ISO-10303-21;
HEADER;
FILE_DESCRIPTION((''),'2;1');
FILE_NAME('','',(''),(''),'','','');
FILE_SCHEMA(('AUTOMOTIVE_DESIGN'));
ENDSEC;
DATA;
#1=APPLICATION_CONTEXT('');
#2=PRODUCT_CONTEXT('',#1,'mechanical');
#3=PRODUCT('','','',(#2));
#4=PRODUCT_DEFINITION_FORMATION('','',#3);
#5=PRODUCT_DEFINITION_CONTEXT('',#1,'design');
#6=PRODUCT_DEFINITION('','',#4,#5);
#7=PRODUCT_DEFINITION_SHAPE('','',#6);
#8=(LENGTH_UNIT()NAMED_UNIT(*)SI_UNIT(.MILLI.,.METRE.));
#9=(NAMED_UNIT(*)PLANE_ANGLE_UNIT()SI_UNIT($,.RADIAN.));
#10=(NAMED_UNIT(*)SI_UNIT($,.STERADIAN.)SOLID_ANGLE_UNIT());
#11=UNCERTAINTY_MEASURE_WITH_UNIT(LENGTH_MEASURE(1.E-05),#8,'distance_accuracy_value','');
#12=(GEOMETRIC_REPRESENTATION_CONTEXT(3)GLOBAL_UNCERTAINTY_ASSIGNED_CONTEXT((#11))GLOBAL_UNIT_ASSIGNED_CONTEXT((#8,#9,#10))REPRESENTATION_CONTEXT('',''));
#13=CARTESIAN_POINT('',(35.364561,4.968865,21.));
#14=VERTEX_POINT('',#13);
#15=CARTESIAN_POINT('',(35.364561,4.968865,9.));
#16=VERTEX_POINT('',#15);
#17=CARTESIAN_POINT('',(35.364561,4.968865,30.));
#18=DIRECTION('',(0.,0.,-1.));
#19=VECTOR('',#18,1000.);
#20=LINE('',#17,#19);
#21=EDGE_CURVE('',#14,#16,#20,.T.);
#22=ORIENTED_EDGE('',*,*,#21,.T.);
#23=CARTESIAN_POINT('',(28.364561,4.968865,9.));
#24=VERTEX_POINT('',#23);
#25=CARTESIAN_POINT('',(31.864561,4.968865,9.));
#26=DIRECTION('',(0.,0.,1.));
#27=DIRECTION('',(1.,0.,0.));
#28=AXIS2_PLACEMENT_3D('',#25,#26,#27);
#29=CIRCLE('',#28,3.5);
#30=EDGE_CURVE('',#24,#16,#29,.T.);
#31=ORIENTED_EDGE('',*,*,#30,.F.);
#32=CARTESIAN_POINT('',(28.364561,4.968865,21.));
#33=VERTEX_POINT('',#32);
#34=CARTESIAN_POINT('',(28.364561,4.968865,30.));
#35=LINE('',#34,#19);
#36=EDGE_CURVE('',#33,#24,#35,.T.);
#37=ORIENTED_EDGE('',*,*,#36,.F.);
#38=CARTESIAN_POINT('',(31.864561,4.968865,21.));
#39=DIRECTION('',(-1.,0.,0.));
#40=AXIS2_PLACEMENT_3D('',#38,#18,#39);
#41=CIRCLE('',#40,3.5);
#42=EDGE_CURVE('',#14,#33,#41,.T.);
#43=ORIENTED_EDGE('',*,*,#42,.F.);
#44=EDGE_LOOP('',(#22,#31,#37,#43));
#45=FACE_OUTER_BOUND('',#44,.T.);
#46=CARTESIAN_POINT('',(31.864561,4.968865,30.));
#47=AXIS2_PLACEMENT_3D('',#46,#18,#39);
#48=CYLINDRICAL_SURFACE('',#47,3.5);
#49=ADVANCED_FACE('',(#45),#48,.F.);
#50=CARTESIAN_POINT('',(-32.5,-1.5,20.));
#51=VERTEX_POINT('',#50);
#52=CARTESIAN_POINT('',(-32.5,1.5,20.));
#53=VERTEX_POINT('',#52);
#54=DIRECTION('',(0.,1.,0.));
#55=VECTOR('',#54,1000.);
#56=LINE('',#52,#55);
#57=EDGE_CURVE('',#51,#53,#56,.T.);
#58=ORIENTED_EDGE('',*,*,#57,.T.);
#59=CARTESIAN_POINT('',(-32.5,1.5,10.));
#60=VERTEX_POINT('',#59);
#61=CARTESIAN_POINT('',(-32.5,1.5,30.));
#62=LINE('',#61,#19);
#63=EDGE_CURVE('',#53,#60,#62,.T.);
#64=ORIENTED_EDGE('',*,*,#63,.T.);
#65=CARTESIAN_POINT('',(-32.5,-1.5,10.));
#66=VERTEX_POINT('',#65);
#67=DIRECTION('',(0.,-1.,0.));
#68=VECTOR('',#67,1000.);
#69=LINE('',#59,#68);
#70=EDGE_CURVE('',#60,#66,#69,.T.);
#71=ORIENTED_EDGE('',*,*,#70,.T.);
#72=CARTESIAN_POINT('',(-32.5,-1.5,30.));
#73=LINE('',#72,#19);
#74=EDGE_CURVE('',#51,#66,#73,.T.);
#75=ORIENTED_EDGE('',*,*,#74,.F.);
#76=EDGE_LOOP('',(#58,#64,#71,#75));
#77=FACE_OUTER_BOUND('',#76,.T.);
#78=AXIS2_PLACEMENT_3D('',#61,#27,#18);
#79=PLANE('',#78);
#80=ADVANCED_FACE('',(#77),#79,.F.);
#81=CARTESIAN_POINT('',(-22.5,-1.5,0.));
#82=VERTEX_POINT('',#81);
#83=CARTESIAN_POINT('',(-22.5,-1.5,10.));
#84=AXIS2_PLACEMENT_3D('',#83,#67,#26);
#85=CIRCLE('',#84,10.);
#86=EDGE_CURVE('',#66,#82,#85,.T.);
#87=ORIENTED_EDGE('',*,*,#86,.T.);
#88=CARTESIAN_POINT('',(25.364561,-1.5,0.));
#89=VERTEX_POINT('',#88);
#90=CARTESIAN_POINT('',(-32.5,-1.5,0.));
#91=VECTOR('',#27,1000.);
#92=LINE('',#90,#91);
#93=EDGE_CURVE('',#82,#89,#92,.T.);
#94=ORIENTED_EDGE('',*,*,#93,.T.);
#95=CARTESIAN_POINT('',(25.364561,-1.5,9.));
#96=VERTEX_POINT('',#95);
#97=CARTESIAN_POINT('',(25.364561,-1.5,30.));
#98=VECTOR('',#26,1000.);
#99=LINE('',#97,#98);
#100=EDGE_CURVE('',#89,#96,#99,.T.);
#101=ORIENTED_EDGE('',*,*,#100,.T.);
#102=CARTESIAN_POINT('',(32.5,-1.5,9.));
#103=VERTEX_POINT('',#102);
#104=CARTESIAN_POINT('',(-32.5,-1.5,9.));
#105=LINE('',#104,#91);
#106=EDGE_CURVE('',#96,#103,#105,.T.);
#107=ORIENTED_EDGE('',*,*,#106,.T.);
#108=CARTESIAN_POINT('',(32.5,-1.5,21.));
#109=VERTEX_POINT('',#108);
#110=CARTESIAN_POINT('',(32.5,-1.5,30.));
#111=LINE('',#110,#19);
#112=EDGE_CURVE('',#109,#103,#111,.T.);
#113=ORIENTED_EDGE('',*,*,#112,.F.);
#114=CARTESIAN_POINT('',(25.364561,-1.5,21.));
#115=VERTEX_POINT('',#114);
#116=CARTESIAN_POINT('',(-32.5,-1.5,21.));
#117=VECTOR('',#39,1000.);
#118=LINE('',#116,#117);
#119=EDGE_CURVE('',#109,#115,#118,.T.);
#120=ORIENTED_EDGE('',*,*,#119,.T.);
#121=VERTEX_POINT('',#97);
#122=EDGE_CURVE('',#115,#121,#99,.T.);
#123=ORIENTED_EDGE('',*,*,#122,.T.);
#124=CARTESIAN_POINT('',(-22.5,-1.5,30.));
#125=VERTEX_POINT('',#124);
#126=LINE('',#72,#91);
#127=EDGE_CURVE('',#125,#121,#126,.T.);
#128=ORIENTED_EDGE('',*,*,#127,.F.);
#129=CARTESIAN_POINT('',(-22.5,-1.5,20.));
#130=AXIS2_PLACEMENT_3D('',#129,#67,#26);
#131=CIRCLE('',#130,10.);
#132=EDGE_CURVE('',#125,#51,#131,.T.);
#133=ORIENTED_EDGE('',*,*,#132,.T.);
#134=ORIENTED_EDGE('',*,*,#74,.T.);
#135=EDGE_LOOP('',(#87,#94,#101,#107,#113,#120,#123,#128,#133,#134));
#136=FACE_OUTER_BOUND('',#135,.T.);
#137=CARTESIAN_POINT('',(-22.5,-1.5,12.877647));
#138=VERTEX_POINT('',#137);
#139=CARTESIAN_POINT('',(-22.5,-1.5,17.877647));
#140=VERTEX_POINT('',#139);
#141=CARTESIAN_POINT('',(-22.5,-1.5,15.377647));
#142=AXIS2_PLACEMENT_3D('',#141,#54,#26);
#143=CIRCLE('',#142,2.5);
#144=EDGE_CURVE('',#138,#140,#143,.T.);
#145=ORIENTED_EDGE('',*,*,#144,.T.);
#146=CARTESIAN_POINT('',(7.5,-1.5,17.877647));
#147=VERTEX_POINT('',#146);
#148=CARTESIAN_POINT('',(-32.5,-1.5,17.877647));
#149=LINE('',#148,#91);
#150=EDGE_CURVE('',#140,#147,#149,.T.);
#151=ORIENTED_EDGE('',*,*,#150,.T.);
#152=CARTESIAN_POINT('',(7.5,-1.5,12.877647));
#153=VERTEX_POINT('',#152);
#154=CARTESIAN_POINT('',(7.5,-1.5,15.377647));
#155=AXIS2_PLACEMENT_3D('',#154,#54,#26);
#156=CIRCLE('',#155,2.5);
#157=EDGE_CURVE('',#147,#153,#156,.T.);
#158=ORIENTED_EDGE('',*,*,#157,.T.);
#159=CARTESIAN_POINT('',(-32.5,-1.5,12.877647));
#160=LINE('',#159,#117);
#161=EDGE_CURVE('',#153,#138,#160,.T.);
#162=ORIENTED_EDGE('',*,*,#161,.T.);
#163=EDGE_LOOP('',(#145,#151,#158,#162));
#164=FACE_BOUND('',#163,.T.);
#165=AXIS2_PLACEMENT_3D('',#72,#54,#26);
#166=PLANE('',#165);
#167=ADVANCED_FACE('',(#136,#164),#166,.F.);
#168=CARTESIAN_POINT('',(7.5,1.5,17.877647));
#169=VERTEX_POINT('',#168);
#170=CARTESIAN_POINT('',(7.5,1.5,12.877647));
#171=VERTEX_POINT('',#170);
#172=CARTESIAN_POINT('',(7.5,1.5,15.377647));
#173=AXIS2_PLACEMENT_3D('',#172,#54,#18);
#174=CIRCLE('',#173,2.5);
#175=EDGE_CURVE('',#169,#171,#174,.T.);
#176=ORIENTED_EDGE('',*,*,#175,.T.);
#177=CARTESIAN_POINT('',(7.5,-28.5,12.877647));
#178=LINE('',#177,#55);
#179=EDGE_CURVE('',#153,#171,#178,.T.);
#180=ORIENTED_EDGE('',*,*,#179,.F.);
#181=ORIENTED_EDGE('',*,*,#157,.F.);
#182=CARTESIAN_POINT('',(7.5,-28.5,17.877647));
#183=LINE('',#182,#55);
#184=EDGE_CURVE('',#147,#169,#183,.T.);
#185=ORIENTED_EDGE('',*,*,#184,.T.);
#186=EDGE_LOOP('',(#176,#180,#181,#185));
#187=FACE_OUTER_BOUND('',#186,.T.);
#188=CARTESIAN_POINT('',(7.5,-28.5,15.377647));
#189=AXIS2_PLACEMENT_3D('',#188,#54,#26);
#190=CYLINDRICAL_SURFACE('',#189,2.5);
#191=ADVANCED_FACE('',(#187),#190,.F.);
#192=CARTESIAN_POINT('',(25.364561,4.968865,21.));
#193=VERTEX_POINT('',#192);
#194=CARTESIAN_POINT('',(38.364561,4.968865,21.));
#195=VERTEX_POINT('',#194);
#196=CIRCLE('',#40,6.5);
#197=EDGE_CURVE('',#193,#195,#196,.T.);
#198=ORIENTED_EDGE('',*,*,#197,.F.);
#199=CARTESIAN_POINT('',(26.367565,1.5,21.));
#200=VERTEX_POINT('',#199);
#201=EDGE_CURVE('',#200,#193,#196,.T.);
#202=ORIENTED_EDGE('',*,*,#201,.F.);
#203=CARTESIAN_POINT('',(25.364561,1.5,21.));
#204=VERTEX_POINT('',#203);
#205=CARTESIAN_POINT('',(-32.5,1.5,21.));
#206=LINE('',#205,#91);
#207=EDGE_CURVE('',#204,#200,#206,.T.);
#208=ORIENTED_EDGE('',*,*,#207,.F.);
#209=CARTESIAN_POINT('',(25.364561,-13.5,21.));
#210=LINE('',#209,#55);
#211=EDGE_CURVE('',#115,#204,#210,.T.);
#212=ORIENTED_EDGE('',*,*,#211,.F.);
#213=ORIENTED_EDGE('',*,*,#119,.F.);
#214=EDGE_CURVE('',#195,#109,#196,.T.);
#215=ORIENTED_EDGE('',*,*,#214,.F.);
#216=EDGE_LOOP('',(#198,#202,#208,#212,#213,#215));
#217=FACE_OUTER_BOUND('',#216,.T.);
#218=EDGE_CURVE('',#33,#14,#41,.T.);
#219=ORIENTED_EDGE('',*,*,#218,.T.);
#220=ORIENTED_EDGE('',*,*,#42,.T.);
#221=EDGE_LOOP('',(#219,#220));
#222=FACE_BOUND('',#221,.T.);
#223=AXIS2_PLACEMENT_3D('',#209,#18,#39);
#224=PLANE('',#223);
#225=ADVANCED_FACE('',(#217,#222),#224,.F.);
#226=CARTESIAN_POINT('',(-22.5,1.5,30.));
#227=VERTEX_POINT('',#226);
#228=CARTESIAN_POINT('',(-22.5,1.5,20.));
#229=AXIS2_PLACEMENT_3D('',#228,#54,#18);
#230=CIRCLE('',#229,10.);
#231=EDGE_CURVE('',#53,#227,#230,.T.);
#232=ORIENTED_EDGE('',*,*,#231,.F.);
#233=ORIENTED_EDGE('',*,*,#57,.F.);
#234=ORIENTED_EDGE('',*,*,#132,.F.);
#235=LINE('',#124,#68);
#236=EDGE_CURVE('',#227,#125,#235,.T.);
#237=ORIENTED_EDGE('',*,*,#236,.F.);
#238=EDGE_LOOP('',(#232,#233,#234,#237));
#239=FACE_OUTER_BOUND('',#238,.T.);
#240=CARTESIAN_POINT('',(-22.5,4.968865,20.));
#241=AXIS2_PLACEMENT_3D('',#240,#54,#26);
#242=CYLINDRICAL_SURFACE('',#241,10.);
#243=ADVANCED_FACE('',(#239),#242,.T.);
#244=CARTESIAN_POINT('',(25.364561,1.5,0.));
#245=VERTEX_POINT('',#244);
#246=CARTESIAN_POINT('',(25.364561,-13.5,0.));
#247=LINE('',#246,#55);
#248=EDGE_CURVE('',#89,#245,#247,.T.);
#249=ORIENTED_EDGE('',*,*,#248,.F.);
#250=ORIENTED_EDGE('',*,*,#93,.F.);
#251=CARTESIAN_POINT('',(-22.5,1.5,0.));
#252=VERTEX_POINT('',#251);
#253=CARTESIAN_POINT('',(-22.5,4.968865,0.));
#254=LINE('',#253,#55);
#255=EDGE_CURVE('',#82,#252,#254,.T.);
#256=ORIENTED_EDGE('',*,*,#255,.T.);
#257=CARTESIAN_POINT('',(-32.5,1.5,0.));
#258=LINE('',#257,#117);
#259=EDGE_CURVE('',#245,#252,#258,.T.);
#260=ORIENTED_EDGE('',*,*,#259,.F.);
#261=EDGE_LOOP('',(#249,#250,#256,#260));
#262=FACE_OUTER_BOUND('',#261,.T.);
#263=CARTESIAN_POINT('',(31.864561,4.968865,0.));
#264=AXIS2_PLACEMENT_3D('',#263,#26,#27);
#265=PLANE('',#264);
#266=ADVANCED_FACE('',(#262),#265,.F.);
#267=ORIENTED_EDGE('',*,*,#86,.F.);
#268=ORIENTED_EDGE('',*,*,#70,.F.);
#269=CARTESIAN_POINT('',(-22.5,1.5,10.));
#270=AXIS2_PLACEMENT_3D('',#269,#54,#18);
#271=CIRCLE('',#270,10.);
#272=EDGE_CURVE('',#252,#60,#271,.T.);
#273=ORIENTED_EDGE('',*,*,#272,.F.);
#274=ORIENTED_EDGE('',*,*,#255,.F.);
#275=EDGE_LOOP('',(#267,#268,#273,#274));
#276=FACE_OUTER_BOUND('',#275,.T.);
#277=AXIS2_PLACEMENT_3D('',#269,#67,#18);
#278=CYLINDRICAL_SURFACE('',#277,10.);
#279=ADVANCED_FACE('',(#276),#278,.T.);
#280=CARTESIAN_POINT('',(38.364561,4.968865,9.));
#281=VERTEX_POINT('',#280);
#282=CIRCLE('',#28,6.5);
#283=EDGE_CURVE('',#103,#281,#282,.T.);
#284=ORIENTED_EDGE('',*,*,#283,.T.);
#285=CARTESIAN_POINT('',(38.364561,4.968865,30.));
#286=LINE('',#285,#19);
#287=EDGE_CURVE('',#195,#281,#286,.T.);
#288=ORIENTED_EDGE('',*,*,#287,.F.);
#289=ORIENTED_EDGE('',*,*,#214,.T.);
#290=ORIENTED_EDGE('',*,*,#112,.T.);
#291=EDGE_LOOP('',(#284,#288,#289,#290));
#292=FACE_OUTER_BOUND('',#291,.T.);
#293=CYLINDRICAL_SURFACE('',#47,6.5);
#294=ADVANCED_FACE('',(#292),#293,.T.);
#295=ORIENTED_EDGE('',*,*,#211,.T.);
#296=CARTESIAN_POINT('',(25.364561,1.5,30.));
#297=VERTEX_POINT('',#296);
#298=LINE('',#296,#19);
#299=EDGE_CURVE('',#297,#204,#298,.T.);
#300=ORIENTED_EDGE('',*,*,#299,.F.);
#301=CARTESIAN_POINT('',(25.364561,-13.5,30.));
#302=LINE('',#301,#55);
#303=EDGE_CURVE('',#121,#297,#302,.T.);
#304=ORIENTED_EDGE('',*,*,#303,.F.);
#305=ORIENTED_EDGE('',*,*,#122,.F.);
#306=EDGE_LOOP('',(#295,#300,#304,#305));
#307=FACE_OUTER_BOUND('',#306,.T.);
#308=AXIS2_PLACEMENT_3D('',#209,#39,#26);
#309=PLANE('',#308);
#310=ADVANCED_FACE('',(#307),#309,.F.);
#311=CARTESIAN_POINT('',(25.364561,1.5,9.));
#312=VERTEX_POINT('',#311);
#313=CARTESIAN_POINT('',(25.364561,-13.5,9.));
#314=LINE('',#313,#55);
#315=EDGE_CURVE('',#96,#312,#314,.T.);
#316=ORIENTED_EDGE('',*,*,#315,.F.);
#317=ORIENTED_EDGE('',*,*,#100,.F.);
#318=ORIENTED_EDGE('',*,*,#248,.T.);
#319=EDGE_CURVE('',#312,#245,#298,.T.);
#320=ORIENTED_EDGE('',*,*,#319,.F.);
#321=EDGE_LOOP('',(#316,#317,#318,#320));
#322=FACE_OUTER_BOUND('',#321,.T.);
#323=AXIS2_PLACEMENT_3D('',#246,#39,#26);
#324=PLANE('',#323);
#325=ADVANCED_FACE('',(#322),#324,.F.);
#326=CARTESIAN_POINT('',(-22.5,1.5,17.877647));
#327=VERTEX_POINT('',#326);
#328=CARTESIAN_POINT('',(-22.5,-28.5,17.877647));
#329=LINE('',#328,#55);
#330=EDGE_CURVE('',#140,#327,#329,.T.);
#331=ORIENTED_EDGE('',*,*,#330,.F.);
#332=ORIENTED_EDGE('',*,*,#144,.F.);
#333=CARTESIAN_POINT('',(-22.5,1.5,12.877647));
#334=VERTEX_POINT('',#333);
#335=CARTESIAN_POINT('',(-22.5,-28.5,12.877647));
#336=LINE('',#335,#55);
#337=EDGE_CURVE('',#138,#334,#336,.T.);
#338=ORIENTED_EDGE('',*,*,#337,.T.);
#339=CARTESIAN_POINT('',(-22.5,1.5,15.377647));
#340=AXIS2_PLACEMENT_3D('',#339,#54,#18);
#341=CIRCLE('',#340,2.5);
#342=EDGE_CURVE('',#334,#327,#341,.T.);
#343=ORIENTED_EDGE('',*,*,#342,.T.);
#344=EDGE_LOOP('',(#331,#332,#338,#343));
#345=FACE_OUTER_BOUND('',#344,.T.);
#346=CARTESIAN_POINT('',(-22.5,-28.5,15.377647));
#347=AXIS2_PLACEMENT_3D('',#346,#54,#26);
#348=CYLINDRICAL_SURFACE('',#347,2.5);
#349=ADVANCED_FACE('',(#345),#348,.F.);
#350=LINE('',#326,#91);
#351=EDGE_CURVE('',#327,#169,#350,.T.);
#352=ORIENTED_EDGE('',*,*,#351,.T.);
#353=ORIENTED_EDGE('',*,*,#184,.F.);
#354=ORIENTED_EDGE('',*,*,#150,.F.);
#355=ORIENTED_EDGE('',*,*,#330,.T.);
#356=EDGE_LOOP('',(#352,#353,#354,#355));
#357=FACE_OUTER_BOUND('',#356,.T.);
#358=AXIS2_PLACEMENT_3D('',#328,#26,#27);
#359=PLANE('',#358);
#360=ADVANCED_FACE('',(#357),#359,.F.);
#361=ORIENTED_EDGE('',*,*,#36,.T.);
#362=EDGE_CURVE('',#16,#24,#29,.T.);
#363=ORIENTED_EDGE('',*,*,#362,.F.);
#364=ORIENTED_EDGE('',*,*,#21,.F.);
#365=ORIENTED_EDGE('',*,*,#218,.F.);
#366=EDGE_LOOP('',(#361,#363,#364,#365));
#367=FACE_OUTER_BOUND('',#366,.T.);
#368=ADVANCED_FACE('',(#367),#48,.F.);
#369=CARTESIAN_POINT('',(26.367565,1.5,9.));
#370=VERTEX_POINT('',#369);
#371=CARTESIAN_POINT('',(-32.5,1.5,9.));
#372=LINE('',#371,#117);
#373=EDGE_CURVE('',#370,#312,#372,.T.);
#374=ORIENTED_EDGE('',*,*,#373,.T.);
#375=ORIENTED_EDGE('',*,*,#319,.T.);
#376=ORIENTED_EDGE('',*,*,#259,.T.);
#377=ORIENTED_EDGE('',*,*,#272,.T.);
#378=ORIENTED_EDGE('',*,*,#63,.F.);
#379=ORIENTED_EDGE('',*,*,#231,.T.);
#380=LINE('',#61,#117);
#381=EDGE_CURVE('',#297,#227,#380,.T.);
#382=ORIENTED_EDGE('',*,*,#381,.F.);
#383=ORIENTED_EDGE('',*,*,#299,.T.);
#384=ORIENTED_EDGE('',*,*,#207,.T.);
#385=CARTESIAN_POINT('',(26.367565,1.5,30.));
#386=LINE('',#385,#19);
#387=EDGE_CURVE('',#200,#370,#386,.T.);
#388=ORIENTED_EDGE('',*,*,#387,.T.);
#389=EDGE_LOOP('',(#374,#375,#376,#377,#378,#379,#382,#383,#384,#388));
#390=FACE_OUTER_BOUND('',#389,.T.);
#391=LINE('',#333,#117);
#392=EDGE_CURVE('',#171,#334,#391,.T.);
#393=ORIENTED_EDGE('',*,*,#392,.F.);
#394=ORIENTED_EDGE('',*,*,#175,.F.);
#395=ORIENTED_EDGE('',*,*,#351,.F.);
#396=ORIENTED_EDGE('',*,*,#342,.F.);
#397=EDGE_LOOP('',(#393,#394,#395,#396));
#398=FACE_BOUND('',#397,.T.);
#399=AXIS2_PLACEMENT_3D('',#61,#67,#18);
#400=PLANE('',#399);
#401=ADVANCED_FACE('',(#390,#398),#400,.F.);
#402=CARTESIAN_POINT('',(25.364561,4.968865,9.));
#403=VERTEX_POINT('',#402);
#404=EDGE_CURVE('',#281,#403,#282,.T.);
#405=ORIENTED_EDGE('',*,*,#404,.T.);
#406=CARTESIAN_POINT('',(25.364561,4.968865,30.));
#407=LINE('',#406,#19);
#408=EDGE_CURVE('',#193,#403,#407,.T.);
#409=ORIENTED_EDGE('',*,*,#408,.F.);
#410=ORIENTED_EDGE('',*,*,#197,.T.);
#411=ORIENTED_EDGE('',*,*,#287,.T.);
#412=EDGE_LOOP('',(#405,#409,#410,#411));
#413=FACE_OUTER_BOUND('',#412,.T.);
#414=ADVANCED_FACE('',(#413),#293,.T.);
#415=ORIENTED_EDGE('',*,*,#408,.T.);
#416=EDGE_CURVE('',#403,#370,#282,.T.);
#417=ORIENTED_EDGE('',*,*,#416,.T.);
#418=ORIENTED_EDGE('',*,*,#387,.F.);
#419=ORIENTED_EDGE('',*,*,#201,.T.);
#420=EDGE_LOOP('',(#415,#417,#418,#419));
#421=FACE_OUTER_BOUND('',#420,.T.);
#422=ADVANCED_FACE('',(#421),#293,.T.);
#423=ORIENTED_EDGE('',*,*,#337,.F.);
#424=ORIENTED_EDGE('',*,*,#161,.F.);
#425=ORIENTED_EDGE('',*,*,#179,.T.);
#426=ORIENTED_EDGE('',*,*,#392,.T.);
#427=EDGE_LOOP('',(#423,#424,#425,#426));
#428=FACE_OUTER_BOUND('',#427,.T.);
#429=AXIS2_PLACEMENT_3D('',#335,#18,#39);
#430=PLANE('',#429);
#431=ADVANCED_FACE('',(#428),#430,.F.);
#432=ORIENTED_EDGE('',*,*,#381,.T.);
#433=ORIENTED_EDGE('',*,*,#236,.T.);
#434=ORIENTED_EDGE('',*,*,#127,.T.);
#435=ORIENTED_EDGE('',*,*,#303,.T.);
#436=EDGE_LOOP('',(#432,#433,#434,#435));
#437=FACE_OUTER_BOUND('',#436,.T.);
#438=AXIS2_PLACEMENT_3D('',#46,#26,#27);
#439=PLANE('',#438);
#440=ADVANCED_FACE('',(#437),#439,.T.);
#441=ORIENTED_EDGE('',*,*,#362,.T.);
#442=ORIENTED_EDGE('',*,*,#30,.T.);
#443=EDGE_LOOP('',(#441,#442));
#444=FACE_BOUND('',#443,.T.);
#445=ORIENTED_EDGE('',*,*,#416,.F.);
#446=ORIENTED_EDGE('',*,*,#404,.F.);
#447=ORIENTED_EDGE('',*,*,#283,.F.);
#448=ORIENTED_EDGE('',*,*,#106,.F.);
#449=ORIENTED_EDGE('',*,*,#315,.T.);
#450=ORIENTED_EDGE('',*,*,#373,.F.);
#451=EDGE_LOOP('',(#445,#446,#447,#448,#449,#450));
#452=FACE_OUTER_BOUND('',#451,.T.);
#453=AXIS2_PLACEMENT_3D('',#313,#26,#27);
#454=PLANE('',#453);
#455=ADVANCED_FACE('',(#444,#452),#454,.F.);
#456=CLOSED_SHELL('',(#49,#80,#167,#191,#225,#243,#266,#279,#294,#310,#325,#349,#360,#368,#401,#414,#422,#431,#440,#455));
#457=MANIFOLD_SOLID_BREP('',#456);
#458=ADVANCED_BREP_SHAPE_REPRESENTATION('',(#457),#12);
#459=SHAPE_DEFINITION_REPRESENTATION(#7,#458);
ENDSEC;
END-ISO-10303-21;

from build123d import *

# Parameters (mm, degrees)
SKETCH_1_R          = 3.5
EXTRUDE_1_DEPTH     = 30
FILLET_1_R          = 10
CUT_EXTRUDE_1_DEPTH = 30
SKETCH_3_W          = 18.572765592
SKETCH_3_H          = 9
SKETCH_3_W_2        = 28.522519482
CUT_EXTRUDE_2_DEPTH = 15


with BuildPart() as part:
    # 草图1 → 凸台-拉伸1 (new body)
    with BuildSketch(Plane.XY):
        with BuildLine():
            Line((-32.5, 1.5), (26.367564687, 1.5))
            ThreePointArc((26.367564687, 1.5), (34.720903057, 10.807641922), (32.5, -1.5))
            Line((32.5, -1.5), (-32.5, -1.5))
            Line((-32.5, -1.5), (-32.5, 1.5))
        make_face()
        with Locations((31.86456148, 4.96886527)):
            Circle(SKETCH_1_R, mode=Mode.SUBTRACT)
    extrude(amount=EXTRUDE_1_DEPTH)

    # 圆角1
    fillet_1_edges = [part.edges().sort_by_distance(p)[0] for p in [
        (-32.5, 0, 30),
        (-32.5, 0, 0),
    ]]
    fillet(fillet_1_edges, radius=FILLET_1_R)

    # 草图2 → 切除-拉伸1 (cut)
    with BuildSketch(Plane(origin=(0, 1.5, 0), x_dir=(1, 0, 0), z_dir=(0, 1, 0))):
        with BuildLine():
            Line((-22.5, -12.87764733), (7.5, -12.87764733))
            ThreePointArc((7.5, -12.87764733), (10, -15.37764733), (7.5, -17.87764733))
            Line((7.5, -17.87764733), (-22.5, -17.87764733))
            ThreePointArc((-22.5, -17.87764733), (-25, -15.37764733), (-22.5, -12.87764733))
        make_face()
    extrude(amount=-CUT_EXTRUDE_1_DEPTH, mode=Mode.SUBTRACT)

    # 草图3 → 切除-拉伸2 (cut, symmetric)
    with BuildSketch(Plane(origin=(0, 1.5, 0), x_dir=(1, 0, 0), z_dir=(0, 1, 0))):
        with Locations((34.650944276, -25.5)):
            Rectangle(SKETCH_3_W, SKETCH_3_H)
        with Locations((39.625821221, -4.5)):
            Rectangle(SKETCH_3_W_2, SKETCH_3_H)
    extrude(amount=CUT_EXTRUDE_2_DEPTH, both=True, mode=Mode.SUBTRACT)


solid = part.part
